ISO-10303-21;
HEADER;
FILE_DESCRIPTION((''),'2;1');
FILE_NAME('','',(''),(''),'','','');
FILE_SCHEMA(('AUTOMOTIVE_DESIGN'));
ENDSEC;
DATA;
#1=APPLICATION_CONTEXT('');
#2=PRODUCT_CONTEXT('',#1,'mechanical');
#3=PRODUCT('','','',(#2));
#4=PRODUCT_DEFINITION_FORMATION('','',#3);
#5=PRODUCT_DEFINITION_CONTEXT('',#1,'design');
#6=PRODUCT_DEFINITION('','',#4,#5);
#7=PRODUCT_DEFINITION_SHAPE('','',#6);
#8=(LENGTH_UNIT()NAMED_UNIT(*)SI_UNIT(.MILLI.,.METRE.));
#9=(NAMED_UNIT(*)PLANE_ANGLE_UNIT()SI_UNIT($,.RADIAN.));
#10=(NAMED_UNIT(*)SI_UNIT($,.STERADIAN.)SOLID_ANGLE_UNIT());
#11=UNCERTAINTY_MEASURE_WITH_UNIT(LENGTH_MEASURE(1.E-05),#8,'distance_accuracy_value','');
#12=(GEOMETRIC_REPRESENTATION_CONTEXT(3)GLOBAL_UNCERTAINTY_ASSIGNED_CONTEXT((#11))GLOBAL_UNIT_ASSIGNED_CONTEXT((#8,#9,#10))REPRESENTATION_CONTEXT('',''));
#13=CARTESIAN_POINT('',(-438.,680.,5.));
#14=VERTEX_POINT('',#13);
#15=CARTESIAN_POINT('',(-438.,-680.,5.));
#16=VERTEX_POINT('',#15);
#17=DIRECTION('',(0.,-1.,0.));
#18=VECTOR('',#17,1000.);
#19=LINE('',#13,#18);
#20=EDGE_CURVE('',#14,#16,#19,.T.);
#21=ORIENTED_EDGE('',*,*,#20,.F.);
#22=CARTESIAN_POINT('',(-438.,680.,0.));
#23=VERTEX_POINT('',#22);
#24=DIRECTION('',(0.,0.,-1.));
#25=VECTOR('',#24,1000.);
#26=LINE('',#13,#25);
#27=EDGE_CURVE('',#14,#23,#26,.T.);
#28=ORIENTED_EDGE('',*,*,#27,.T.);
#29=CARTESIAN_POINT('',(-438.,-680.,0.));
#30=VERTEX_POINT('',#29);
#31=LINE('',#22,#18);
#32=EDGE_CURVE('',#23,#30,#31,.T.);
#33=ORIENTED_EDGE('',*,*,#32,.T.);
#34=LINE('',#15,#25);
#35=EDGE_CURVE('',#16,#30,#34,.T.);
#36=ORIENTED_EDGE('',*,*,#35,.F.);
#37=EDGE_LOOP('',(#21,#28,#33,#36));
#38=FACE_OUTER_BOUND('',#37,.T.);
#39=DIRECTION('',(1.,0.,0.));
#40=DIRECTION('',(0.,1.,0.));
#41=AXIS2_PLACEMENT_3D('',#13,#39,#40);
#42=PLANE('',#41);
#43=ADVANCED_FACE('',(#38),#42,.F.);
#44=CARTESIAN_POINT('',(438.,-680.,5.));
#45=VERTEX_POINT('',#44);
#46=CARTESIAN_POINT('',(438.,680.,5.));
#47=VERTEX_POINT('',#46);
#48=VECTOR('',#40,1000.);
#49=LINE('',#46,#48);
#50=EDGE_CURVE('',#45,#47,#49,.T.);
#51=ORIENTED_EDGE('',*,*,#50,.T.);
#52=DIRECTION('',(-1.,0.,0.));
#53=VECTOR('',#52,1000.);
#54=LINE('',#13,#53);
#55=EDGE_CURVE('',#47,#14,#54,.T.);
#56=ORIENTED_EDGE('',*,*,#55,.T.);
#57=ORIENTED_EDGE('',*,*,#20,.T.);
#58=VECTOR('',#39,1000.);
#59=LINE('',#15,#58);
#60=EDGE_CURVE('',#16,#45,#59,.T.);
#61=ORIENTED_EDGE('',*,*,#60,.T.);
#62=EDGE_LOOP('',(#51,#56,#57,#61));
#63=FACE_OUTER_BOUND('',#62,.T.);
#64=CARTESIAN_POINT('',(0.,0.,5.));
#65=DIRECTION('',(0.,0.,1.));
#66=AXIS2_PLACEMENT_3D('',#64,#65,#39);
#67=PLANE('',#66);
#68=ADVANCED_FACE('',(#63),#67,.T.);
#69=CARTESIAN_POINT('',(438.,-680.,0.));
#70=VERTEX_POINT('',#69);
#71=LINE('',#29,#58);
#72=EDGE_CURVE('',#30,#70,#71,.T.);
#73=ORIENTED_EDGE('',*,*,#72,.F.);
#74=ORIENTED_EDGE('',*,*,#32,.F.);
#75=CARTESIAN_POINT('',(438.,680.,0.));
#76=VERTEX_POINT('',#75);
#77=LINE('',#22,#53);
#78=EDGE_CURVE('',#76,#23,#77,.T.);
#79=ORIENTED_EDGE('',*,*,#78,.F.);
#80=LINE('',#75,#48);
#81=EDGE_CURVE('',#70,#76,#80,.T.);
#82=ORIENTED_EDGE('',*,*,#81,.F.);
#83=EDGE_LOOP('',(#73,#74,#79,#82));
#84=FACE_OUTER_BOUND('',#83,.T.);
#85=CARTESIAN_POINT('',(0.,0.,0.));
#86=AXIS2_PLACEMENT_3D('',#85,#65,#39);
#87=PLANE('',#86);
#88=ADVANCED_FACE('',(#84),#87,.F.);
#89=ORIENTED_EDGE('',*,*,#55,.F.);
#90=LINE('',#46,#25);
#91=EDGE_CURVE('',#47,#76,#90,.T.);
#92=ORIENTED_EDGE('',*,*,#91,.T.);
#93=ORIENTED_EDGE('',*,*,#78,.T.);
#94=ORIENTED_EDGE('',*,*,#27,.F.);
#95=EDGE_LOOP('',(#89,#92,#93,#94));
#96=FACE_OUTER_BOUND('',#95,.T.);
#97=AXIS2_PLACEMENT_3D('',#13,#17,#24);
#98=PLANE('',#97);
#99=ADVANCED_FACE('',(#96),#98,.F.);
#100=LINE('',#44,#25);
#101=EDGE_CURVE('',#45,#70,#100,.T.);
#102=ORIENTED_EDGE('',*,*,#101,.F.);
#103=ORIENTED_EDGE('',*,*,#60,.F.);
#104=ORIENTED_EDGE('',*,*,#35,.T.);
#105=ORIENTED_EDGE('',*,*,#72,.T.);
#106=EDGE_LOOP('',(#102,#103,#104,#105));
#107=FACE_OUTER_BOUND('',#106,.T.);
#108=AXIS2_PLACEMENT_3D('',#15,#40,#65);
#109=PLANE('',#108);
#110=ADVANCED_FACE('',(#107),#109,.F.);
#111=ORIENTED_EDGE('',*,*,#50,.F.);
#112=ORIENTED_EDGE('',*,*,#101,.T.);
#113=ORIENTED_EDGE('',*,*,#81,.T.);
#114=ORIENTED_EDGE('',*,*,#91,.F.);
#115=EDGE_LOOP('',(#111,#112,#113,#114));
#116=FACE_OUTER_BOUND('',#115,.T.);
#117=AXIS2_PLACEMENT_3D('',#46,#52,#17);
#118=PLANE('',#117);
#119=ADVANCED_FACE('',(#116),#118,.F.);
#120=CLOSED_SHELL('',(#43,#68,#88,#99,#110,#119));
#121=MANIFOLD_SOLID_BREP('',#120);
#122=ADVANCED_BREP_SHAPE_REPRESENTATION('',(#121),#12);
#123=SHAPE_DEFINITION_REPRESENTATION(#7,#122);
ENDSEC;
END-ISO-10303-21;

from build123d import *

# Parameters (mm, degrees)
SKETCH_1_W      = 876
SKETCH_1_H      = 1360
EXTRUDE_1_DEPTH = 5


with BuildPart() as part:
    # 草图1 → 凸台-拉伸1 (new body)
    with BuildSketch(Plane.XY):
        Rectangle(SKETCH_1_W, SKETCH_1_H)
    extrude(amount=EXTRUDE_1_DEPTH)


solid = part.part
